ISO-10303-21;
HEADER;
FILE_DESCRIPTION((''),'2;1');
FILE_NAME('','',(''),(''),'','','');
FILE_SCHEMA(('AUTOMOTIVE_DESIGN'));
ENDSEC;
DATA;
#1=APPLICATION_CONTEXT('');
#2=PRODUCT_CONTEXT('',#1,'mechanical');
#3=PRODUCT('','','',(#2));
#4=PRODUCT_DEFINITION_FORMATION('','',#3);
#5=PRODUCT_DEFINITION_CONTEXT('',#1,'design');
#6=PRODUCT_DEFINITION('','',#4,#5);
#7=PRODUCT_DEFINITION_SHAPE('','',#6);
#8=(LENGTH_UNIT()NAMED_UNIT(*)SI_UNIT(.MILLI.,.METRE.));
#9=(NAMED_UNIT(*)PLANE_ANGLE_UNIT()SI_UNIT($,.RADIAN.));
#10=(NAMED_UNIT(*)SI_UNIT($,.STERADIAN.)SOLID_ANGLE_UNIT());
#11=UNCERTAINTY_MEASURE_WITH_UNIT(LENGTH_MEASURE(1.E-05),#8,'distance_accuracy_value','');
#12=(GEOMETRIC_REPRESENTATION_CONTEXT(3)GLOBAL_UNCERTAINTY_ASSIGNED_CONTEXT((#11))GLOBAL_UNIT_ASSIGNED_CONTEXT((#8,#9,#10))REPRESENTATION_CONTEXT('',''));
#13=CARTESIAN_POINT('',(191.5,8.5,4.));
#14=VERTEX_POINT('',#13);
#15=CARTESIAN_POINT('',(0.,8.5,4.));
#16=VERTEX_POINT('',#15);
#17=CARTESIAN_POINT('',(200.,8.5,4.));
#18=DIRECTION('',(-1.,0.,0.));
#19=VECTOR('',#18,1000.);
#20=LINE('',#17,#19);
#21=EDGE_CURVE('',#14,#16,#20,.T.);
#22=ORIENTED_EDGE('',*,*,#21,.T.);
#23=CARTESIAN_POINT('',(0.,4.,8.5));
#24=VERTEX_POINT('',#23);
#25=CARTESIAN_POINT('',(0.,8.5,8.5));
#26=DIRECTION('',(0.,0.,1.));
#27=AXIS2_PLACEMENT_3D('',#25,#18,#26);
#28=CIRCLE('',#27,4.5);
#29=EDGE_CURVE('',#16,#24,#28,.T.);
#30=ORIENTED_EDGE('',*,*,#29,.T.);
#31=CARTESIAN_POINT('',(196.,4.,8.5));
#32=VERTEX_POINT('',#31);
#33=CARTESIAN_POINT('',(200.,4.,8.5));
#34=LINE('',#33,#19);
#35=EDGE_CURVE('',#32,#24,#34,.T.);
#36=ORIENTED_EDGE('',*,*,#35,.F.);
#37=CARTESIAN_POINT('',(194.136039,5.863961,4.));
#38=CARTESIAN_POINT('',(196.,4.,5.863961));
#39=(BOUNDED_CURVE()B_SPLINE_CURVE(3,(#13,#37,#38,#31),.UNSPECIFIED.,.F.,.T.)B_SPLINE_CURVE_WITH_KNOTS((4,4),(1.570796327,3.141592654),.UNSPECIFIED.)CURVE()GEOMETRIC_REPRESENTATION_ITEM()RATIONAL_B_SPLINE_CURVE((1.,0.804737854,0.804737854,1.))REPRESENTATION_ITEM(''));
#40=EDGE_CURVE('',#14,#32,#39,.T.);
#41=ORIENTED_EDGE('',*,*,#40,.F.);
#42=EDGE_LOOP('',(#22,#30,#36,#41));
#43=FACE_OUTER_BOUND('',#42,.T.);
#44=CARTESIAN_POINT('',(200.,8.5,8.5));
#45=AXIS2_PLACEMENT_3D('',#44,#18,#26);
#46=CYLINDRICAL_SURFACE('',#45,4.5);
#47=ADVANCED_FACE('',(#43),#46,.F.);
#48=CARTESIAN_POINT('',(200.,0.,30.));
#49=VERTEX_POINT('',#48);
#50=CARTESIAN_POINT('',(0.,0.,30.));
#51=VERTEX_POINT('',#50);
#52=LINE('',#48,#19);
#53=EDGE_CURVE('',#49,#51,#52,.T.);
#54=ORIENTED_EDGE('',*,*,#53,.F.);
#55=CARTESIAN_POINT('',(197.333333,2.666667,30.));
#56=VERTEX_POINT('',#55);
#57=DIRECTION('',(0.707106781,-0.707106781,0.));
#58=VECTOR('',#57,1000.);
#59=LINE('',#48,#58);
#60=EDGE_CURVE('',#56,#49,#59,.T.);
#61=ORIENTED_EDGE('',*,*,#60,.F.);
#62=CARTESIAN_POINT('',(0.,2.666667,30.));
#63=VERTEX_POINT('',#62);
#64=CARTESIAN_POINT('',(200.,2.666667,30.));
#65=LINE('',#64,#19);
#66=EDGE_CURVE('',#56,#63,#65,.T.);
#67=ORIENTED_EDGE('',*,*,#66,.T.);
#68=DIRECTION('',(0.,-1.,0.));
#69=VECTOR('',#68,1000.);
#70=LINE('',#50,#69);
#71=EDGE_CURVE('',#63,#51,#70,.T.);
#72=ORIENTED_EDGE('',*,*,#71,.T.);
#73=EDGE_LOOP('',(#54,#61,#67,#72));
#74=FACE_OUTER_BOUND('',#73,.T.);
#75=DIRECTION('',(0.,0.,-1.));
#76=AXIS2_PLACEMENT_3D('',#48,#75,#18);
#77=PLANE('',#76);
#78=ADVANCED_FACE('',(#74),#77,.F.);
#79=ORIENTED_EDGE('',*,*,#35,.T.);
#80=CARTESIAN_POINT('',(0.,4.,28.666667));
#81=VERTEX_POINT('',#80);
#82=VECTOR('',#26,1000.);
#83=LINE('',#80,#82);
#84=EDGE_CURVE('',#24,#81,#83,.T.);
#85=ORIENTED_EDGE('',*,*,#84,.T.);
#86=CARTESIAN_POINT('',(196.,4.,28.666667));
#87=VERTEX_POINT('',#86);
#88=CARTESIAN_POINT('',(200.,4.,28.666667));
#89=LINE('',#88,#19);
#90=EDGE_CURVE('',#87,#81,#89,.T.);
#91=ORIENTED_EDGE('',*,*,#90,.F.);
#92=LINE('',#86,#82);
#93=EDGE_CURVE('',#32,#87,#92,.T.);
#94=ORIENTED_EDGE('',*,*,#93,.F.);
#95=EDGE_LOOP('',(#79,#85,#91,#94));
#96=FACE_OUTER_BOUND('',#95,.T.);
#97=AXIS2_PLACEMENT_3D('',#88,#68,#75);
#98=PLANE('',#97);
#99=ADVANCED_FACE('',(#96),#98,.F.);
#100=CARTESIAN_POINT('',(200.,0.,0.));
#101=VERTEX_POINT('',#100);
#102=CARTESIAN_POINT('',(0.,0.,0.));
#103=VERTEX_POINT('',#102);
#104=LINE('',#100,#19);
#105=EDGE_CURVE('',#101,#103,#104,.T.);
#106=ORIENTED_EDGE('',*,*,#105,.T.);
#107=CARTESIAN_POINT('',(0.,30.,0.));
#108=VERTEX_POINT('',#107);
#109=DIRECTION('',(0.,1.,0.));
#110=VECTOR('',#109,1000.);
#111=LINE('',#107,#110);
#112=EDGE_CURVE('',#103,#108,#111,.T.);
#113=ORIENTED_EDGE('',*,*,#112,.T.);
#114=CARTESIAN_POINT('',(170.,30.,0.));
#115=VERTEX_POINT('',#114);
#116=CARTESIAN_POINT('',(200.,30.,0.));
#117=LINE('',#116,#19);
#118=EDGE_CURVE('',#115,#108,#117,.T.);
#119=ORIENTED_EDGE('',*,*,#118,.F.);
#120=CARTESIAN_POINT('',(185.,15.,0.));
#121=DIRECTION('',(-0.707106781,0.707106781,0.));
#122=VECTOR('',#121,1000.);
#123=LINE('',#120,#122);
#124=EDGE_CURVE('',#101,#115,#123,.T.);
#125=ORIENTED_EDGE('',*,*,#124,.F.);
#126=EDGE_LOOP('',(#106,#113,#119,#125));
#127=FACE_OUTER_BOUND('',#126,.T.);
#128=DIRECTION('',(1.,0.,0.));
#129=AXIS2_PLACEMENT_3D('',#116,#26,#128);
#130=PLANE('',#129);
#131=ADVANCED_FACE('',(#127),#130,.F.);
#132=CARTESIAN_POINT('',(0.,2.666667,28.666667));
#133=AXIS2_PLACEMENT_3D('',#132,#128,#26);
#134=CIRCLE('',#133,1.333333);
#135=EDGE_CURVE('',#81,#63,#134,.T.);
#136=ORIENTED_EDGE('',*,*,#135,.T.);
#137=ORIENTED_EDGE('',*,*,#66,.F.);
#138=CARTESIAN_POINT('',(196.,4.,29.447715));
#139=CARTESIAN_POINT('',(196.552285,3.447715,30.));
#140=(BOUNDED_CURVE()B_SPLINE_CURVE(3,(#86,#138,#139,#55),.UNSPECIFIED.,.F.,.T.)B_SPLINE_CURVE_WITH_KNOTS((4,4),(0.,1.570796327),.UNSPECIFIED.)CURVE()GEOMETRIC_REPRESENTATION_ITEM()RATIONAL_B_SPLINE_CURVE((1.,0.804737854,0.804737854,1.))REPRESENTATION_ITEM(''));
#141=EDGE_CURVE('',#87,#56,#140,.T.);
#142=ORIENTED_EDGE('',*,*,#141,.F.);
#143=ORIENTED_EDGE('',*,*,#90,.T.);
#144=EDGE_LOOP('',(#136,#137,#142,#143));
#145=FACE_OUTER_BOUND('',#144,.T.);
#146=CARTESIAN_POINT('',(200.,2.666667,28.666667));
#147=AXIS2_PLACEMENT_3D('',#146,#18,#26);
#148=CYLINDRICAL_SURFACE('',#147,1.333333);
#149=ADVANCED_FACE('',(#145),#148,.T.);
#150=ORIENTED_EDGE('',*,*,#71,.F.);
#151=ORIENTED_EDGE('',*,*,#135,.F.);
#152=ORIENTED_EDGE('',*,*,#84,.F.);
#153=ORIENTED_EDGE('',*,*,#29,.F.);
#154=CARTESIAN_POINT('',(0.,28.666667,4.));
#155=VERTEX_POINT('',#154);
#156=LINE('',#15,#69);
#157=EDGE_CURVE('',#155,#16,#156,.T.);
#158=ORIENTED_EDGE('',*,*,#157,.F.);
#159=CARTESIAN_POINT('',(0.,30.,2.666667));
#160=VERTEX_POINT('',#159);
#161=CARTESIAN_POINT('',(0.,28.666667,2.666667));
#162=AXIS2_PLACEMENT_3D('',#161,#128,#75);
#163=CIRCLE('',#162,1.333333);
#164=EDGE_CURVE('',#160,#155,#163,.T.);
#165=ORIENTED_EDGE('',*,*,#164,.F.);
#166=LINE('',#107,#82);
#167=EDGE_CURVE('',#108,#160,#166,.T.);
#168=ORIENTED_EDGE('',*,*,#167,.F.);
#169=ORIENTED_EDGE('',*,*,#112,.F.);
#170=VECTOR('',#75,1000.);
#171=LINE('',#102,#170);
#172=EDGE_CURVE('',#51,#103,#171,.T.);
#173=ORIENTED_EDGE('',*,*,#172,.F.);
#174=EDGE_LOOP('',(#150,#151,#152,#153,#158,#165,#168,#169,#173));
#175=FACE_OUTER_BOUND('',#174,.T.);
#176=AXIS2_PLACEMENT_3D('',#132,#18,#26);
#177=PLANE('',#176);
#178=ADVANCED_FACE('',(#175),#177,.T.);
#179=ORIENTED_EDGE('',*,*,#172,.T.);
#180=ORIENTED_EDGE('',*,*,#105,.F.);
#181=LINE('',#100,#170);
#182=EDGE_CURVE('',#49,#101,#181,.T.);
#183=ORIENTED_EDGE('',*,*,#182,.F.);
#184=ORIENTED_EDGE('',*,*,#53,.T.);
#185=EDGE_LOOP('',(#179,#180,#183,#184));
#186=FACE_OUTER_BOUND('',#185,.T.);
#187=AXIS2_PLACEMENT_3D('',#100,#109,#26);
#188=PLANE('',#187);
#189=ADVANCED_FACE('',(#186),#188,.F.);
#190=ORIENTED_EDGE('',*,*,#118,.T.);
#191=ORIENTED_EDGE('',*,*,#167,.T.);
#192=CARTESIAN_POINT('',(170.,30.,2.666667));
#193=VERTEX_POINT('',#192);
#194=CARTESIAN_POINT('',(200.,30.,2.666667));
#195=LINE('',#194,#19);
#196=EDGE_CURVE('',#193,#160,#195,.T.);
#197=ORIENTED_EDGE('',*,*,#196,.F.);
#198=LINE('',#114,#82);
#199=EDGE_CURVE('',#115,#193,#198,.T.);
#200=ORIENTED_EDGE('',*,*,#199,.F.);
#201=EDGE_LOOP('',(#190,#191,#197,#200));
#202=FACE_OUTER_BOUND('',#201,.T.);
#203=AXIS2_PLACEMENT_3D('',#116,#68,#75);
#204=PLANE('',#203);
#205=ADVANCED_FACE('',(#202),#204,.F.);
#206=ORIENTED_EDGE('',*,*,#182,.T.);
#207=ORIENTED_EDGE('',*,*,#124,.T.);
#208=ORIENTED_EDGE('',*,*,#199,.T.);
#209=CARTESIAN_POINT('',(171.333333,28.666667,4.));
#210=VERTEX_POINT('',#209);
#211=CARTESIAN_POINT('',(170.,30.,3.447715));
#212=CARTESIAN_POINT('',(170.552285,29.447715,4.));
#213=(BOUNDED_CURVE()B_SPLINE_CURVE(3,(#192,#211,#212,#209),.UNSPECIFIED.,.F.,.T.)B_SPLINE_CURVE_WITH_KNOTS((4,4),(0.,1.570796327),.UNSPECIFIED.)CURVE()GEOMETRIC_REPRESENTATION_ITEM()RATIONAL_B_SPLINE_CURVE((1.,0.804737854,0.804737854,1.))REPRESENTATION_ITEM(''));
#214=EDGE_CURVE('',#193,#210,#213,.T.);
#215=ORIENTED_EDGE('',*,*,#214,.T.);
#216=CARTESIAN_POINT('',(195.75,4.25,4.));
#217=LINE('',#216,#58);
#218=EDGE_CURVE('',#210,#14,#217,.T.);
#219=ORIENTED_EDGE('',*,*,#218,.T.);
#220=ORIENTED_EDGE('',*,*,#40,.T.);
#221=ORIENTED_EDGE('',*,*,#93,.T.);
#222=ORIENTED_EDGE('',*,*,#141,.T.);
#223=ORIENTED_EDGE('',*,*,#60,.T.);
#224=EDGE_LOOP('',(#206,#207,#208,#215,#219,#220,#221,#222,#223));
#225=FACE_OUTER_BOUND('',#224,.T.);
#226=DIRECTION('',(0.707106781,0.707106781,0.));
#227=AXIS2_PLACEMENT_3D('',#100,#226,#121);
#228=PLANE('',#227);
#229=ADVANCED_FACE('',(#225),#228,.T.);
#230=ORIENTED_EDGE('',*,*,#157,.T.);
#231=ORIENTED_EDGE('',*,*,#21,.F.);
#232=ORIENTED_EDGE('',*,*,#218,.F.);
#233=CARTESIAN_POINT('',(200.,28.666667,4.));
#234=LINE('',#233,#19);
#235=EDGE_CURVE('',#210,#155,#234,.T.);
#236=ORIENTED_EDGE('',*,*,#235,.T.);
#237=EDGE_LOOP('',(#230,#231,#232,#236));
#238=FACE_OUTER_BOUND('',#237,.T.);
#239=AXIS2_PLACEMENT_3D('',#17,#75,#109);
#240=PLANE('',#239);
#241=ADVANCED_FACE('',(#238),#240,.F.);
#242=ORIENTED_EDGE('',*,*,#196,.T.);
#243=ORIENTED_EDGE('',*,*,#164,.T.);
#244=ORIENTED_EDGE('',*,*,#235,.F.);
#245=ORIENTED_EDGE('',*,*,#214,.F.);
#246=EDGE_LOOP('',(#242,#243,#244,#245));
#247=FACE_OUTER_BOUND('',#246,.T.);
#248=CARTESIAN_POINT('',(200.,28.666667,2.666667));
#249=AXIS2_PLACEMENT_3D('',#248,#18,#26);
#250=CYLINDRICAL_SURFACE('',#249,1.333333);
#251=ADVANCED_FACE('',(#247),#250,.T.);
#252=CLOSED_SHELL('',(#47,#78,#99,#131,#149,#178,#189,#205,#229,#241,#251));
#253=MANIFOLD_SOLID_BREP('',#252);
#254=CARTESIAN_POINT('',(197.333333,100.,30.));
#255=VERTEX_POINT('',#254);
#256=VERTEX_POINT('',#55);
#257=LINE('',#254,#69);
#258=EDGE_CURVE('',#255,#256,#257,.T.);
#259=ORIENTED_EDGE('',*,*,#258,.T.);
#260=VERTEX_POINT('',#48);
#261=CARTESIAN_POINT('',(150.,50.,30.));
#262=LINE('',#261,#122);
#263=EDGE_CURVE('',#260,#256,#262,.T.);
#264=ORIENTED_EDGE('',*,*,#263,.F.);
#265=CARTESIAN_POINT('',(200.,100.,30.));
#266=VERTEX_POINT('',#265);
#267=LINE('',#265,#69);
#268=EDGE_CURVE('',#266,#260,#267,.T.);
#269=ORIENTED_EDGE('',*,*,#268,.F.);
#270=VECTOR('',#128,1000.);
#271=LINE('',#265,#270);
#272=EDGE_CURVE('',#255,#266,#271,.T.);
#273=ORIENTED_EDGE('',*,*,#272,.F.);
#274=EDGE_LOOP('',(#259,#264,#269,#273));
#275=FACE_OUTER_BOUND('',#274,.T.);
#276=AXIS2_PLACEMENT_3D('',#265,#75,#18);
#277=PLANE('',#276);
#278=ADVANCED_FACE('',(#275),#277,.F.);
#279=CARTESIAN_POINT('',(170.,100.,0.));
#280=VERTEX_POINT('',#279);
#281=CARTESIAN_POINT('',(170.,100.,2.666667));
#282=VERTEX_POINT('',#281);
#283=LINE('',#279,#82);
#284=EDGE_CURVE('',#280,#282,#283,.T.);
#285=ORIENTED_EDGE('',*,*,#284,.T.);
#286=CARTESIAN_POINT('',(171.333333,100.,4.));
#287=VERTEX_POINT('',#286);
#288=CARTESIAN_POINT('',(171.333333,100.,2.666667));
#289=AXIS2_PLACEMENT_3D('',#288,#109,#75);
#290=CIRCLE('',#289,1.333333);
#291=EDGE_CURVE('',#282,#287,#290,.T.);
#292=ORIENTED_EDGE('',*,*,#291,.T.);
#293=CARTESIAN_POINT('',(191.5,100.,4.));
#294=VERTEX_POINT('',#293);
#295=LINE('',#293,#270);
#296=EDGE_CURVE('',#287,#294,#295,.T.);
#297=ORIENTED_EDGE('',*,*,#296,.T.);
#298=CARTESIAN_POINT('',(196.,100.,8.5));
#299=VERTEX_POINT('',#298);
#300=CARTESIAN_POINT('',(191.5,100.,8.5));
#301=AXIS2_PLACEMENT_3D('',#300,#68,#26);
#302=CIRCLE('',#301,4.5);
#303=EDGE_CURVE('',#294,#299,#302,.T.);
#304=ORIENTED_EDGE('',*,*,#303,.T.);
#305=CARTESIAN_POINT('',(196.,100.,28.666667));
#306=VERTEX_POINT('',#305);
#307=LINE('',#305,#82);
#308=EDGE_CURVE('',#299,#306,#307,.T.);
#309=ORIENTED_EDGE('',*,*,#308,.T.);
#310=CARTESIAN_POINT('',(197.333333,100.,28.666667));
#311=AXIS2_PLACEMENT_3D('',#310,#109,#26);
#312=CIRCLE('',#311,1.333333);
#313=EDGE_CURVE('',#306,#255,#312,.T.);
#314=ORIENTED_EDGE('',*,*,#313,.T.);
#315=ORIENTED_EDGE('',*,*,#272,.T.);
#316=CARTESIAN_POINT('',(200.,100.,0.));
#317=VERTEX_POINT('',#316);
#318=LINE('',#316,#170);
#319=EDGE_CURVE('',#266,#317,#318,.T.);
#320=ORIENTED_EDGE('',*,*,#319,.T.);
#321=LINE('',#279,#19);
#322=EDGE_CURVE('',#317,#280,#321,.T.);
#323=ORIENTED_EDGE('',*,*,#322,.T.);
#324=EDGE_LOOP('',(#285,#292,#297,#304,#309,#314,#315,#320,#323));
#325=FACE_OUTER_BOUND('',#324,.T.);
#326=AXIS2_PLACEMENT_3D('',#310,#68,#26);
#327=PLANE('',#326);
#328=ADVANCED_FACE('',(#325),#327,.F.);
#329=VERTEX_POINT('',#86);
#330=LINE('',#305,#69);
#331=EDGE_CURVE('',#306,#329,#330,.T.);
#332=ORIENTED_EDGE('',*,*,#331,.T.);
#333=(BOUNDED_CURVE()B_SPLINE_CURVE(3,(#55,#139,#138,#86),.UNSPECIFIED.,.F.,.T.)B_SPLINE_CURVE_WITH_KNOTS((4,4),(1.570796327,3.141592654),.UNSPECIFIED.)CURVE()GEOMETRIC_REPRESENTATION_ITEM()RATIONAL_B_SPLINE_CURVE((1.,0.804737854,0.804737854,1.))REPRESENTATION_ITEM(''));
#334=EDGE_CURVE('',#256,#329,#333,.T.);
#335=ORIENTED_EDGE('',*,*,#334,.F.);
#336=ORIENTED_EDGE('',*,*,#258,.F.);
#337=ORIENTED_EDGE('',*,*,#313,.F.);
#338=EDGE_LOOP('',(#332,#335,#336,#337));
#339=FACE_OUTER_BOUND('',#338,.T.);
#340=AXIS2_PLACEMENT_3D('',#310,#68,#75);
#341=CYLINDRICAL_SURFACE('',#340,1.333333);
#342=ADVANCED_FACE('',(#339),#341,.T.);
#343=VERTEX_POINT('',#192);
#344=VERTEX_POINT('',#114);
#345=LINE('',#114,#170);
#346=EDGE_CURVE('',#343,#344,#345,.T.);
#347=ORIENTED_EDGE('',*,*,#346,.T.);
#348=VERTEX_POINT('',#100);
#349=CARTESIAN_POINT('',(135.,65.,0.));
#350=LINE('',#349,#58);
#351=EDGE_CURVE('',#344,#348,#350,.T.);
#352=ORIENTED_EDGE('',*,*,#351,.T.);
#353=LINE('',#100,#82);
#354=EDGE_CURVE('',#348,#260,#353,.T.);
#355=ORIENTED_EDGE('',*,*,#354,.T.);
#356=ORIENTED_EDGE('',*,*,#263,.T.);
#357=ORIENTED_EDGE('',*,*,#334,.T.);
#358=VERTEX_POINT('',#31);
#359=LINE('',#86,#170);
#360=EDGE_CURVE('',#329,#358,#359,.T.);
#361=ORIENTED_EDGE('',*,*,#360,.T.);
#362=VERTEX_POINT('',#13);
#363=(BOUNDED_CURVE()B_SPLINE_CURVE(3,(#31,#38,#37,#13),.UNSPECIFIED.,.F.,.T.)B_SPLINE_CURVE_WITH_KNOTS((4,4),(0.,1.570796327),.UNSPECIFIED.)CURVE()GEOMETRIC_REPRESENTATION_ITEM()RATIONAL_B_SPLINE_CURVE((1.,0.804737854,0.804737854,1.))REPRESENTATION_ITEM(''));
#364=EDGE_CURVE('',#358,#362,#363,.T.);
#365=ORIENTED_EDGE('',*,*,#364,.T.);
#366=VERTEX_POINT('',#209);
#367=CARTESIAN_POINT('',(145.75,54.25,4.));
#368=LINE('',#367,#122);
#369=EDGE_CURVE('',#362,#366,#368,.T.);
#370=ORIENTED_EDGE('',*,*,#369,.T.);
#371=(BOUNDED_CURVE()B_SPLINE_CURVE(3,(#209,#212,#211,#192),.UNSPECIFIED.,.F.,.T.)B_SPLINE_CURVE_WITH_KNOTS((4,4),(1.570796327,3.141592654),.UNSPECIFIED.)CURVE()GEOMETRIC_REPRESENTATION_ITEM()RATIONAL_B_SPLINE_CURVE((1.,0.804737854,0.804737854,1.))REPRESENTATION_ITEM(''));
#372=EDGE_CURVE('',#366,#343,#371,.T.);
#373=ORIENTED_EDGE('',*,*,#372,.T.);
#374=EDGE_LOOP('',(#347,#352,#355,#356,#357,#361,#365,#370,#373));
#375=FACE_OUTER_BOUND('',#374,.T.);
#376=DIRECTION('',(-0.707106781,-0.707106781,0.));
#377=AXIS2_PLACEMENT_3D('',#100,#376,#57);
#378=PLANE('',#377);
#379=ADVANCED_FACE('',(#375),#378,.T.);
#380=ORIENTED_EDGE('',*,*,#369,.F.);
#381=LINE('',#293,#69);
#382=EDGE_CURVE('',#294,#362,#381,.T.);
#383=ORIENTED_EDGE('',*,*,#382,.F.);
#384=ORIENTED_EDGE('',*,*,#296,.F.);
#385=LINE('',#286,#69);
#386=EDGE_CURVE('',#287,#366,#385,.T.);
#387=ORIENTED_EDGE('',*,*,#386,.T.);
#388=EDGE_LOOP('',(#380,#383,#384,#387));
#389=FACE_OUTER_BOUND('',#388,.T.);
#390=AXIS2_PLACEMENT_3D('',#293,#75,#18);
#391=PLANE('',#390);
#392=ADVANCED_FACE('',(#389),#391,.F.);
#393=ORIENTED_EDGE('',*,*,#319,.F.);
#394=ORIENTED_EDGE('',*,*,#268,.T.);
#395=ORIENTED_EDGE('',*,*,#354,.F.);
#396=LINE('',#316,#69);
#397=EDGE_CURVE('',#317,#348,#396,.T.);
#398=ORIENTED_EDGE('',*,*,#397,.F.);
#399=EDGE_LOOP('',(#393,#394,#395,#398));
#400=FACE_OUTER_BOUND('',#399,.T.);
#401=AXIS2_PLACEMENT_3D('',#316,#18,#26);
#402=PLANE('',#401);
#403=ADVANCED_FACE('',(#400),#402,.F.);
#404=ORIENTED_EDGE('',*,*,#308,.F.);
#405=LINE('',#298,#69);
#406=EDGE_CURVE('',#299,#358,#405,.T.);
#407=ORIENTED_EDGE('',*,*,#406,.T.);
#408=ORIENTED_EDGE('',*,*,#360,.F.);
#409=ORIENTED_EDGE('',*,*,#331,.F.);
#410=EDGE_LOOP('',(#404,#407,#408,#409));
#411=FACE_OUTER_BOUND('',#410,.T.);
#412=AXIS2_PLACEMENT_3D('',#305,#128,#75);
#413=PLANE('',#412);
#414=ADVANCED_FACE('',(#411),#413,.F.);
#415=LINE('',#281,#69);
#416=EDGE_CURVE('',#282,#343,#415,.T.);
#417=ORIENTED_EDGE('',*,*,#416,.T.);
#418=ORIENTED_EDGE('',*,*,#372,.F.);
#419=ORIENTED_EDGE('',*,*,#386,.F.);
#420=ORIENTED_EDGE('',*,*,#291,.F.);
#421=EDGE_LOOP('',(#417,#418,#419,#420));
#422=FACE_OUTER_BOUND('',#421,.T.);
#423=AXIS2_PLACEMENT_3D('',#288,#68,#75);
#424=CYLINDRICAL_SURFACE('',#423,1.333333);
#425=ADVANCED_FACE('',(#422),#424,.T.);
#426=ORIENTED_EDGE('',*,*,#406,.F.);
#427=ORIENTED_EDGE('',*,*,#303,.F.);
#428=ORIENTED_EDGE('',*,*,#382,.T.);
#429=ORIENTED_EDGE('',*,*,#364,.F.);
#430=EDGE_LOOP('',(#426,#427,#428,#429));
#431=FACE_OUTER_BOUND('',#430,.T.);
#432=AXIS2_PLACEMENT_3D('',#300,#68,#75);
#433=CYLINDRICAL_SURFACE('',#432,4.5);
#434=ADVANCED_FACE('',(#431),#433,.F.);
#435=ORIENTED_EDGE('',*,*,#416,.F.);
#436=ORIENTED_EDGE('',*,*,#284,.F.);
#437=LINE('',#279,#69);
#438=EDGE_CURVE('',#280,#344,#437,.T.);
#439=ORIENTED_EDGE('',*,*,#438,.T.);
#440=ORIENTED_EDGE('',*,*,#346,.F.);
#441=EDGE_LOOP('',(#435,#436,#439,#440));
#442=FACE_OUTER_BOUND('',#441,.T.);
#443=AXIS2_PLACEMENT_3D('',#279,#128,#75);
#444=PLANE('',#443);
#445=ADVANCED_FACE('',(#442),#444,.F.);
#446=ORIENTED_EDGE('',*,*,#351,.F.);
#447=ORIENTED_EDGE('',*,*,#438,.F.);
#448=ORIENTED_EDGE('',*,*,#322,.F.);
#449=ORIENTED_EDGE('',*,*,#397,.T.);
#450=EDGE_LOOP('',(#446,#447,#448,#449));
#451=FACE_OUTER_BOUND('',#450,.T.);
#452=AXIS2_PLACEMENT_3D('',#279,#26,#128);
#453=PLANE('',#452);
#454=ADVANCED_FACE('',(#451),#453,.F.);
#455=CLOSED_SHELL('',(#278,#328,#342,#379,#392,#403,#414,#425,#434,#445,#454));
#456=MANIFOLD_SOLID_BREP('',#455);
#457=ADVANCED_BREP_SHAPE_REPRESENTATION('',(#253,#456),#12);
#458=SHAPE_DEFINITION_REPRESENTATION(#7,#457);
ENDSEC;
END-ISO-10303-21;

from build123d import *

# Parameters (mm, degrees)
GBT706_2008_030_4_1_DEPTH   = 243.426406871
GBT706_2008_030_4_1_2_DEPTH = 143.426406871


with BuildPart() as part:
    # Sketch12 → Gbt706-2008 热轧等边角钢 030×4(1) (new body)
    with BuildSketch(Plane.YZ):
        with BuildLine():
            Line((0, 0), (0, 30))
            Line((0, 30), (2.666666667, 30))
            ThreePointArc((2.666666667, 30), (3.609475708, 29.609475708), (4, 28.666666667))
            Line((4, 28.666666667), (4, 8.5))
            ThreePointArc((4, 8.5), (5.318019485, 5.318019485), (8.5, 4))
            Line((8.5, 4), (28.666666667, 4))
            ThreePointArc((28.666666667, 4), (29.609475708, 3.609475708), (30, 2.666666667))
            Line((30, 2.666666667), (30, 0))
            Line((30, 0), (0, 0))
        make_face()
    extrude(amount=GBT706_2008_030_4_1_DEPTH)

    # Gbt706-2008 热轧等边角钢 030×4(1) mitre 1
    split(bisect_by=Plane(origin=(200, 0, 0), x_dir=(0.707106781, -0.707106781, 0), z_dir=(-0.707106781, -0.707106781, 0)), keep=Keep.TOP)


with BuildPart() as body_2:
    # Sketch12 on segment 2 (carried to segment 2) → Gbt706-2008 _ 030_4_1 2 (new body)
    with BuildSketch(Plane(origin=(200, -43.426406871, 0), x_dir=(-1, 0, 0), z_dir=(0, 1, 0))):
        with BuildLine():
            Line((0, 0), (0, 30))
            Line((0, 30), (2.666666667, 30))
            ThreePointArc((2.666666667, 30), (3.609475708, 29.609475708), (4, 28.666666667))
            Line((4, 28.666666667), (4, 8.5))
            ThreePointArc((4, 8.5), (5.318019485, 5.318019485), (8.5, 4))
            Line((8.5, 4), (28.666666667, 4))
            ThreePointArc((28.666666667, 4), (29.609475708, 3.609475708), (30, 2.666666667))
            Line((30, 2.666666667), (30, 0))
            Line((30, 0), (0, 0))
        make_face()
    extrude(amount=GBT706_2008_030_4_1_2_DEPTH)

    # Gbt706-2008 _ 030_4_1 2 mitre 1
    split(bisect_by=Plane(origin=(200, 0, 0), x_dir=(-0.707106781, 0.707106781, 0), z_dir=(0.707106781, 0.707106781, 0)), keep=Keep.TOP)


solid = Compound([part.part, body_2.part])
